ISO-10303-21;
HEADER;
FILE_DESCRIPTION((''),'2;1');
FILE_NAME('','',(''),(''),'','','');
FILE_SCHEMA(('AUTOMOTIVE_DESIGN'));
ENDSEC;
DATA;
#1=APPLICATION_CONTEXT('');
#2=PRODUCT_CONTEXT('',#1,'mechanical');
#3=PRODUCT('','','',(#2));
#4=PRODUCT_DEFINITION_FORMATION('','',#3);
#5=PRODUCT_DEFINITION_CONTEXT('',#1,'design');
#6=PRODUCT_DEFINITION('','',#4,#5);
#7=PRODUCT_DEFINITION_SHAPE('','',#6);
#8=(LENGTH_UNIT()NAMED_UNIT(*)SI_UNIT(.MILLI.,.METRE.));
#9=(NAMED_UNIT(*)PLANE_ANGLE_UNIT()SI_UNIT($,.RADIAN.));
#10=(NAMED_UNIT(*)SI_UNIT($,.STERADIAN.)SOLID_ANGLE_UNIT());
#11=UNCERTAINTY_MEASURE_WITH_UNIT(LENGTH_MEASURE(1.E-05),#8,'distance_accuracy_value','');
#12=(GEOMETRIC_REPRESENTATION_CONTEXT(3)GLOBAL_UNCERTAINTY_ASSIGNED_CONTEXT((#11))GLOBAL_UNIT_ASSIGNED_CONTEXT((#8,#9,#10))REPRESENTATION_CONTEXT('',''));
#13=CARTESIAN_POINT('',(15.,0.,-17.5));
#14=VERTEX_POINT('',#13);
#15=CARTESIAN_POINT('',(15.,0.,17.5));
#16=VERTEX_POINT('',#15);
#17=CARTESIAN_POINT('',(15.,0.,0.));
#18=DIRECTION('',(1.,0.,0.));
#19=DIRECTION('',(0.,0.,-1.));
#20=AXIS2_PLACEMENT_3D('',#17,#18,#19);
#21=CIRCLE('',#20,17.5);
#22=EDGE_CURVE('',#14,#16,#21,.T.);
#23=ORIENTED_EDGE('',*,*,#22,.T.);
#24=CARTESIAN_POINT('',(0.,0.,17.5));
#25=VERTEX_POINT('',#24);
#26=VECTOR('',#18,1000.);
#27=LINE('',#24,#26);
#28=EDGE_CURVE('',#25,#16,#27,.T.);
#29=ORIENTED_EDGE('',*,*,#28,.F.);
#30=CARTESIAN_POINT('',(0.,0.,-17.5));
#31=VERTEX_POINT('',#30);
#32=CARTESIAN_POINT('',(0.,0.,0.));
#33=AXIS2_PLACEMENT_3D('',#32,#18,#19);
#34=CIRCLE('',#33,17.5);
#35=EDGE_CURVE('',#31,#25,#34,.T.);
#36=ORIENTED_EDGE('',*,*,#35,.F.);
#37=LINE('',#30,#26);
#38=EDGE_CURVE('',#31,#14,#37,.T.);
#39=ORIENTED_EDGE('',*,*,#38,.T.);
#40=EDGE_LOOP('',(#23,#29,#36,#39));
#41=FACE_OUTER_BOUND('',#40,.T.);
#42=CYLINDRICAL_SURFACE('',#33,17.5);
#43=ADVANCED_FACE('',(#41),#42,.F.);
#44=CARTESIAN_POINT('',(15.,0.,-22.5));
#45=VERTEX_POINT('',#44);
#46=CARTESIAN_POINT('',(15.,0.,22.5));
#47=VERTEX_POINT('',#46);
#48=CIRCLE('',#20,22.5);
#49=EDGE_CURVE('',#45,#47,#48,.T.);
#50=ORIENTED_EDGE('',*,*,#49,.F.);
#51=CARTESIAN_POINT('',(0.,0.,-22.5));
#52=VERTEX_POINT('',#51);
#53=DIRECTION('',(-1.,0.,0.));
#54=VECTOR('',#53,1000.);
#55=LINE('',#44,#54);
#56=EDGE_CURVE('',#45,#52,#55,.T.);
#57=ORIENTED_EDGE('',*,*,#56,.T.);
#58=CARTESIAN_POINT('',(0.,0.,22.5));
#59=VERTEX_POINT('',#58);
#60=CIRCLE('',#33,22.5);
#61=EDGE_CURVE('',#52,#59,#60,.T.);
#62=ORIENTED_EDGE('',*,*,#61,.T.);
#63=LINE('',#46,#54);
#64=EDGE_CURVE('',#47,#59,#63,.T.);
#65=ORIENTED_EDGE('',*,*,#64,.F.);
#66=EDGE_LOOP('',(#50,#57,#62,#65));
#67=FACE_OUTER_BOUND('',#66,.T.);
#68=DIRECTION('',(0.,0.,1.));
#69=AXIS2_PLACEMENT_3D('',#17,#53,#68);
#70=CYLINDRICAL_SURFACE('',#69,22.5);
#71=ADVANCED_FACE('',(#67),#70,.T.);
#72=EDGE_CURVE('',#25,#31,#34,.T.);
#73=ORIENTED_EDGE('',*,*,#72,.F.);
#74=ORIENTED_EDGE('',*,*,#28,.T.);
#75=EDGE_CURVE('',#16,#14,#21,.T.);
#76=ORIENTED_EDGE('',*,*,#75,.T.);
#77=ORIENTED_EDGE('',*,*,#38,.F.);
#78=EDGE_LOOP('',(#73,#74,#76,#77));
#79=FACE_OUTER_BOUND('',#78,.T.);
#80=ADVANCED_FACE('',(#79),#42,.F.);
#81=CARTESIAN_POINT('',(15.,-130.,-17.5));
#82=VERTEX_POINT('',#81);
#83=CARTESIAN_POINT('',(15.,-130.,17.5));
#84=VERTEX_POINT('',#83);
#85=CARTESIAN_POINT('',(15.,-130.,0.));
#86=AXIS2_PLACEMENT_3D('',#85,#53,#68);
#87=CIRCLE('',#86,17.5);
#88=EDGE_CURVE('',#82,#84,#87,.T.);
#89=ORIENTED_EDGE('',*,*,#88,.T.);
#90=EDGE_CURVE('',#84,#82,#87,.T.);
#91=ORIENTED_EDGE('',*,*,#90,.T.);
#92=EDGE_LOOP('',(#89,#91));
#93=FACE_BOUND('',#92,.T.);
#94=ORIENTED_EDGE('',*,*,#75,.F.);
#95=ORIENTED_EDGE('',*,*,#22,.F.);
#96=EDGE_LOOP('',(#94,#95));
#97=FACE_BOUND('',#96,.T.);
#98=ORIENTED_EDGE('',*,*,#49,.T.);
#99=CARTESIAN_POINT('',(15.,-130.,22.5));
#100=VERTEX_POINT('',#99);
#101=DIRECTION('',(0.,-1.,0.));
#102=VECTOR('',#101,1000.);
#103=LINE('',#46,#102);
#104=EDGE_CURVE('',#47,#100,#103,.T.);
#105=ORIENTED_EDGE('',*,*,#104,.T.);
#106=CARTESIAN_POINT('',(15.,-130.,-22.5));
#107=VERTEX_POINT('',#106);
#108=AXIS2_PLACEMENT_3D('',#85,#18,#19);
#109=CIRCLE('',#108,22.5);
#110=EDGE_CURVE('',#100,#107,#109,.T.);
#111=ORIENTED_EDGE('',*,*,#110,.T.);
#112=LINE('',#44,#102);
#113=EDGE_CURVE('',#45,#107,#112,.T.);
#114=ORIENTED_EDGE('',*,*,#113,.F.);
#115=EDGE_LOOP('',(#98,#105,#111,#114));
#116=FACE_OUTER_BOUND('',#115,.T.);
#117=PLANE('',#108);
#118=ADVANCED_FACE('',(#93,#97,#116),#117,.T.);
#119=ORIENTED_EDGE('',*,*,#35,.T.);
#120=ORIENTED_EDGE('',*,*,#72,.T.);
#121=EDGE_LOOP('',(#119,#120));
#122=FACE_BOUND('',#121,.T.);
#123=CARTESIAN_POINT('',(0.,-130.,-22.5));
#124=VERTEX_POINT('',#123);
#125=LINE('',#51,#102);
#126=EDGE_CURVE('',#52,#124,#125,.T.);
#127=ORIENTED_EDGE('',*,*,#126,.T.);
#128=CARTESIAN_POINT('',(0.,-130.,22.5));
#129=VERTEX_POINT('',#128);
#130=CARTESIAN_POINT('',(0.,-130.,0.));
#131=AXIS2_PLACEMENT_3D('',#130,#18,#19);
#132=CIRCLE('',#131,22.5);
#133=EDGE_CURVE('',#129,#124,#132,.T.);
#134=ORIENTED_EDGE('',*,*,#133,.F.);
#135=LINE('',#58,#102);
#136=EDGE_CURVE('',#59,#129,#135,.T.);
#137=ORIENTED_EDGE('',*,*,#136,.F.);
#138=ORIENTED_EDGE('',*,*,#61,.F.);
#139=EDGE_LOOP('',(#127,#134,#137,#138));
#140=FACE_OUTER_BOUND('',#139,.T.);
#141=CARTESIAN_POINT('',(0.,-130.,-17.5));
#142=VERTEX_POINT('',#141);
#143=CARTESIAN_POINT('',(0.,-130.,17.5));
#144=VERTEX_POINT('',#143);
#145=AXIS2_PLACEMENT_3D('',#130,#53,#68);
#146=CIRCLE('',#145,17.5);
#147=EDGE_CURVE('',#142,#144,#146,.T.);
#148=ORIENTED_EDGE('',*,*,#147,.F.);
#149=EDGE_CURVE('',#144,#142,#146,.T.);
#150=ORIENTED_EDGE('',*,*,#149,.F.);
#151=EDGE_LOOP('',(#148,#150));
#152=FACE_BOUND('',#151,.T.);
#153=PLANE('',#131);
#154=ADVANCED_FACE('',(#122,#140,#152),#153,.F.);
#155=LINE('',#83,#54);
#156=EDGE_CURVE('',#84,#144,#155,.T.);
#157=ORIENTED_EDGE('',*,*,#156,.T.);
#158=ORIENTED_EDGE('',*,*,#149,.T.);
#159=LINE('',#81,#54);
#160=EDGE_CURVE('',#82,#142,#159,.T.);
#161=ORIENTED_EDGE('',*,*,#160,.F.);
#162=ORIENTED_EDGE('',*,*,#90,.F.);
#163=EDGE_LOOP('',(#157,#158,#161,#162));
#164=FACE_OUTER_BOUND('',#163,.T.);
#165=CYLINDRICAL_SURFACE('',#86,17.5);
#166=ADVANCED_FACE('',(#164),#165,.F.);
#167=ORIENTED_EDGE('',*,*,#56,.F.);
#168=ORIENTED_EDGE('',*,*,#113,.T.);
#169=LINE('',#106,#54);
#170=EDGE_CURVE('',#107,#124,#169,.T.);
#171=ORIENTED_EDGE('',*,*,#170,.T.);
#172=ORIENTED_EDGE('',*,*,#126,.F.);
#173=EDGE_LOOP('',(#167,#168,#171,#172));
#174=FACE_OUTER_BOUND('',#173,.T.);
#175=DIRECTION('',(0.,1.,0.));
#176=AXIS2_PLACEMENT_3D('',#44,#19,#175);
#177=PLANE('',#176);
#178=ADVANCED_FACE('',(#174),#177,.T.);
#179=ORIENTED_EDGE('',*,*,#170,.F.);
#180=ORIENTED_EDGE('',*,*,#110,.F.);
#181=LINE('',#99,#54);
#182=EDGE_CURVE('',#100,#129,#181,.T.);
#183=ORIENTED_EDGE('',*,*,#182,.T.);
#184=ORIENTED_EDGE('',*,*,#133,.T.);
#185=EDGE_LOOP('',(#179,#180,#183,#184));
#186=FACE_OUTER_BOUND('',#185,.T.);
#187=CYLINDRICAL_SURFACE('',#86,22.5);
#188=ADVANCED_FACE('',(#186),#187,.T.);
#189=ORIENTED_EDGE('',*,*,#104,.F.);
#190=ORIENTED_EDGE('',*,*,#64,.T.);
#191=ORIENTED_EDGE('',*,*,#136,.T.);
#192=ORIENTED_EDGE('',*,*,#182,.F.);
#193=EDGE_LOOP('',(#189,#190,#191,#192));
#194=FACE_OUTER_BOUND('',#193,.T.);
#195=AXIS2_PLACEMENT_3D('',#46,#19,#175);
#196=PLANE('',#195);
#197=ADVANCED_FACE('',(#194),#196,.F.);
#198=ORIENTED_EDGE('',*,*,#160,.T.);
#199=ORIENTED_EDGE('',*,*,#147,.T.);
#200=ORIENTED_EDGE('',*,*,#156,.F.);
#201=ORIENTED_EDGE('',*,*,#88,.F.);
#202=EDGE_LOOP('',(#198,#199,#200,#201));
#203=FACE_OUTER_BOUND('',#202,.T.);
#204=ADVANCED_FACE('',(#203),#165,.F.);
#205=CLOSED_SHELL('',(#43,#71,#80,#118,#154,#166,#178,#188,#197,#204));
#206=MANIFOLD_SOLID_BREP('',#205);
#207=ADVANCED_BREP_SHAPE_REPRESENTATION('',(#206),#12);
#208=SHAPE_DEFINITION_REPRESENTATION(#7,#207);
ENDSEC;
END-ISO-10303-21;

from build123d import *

# Parameters (mm, degrees)
EXTRUDE_1_DEPTH     = 15
SKETCH_2_R          = 17.5
CUT_EXTRUDE_1_DEPTH = 155.878985017
SKETCH_3_R          = 17.5
CUT_EXTRUDE_2_DEPTH = 155.878985017


with BuildPart() as part:
    # 草图1 → 凸台-拉伸1 (new body)
    with BuildSketch(Plane(origin=(0, 0, 0), x_dir=(0, 0, -1), z_dir=(1, 0, 0))):
        with BuildLine():
            Line((22.5, 0), (22.5, -130))
            ThreePointArc((22.5, -130), (0, -152.5), (-22.5, -130))
            Line((-22.5, -130), (-22.5, 0))
            ThreePointArc((-22.5, 0), (0, 22.5), (22.5, 0))
        make_face()
    extrude(amount=EXTRUDE_1_DEPTH)

    # 草图2 → 切除-拉伸1 (cut, through all)
    with BuildSketch(Plane(origin=(15, 0, 0), x_dir=(0, 0, -1), z_dir=(1, 0, 0))):
        Circle(SKETCH_2_R)
    extrude(amount=-CUT_EXTRUDE_1_DEPTH, mode=Mode.SUBTRACT)

    # 草图3 → 切除-拉伸2 (cut, through all)
    with BuildSketch(Plane.ZY):
        with Locations((0, -130)):
            Circle(SKETCH_3_R)
    extrude(amount=-CUT_EXTRUDE_2_DEPTH, mode=Mode.SUBTRACT)


solid = part.part
